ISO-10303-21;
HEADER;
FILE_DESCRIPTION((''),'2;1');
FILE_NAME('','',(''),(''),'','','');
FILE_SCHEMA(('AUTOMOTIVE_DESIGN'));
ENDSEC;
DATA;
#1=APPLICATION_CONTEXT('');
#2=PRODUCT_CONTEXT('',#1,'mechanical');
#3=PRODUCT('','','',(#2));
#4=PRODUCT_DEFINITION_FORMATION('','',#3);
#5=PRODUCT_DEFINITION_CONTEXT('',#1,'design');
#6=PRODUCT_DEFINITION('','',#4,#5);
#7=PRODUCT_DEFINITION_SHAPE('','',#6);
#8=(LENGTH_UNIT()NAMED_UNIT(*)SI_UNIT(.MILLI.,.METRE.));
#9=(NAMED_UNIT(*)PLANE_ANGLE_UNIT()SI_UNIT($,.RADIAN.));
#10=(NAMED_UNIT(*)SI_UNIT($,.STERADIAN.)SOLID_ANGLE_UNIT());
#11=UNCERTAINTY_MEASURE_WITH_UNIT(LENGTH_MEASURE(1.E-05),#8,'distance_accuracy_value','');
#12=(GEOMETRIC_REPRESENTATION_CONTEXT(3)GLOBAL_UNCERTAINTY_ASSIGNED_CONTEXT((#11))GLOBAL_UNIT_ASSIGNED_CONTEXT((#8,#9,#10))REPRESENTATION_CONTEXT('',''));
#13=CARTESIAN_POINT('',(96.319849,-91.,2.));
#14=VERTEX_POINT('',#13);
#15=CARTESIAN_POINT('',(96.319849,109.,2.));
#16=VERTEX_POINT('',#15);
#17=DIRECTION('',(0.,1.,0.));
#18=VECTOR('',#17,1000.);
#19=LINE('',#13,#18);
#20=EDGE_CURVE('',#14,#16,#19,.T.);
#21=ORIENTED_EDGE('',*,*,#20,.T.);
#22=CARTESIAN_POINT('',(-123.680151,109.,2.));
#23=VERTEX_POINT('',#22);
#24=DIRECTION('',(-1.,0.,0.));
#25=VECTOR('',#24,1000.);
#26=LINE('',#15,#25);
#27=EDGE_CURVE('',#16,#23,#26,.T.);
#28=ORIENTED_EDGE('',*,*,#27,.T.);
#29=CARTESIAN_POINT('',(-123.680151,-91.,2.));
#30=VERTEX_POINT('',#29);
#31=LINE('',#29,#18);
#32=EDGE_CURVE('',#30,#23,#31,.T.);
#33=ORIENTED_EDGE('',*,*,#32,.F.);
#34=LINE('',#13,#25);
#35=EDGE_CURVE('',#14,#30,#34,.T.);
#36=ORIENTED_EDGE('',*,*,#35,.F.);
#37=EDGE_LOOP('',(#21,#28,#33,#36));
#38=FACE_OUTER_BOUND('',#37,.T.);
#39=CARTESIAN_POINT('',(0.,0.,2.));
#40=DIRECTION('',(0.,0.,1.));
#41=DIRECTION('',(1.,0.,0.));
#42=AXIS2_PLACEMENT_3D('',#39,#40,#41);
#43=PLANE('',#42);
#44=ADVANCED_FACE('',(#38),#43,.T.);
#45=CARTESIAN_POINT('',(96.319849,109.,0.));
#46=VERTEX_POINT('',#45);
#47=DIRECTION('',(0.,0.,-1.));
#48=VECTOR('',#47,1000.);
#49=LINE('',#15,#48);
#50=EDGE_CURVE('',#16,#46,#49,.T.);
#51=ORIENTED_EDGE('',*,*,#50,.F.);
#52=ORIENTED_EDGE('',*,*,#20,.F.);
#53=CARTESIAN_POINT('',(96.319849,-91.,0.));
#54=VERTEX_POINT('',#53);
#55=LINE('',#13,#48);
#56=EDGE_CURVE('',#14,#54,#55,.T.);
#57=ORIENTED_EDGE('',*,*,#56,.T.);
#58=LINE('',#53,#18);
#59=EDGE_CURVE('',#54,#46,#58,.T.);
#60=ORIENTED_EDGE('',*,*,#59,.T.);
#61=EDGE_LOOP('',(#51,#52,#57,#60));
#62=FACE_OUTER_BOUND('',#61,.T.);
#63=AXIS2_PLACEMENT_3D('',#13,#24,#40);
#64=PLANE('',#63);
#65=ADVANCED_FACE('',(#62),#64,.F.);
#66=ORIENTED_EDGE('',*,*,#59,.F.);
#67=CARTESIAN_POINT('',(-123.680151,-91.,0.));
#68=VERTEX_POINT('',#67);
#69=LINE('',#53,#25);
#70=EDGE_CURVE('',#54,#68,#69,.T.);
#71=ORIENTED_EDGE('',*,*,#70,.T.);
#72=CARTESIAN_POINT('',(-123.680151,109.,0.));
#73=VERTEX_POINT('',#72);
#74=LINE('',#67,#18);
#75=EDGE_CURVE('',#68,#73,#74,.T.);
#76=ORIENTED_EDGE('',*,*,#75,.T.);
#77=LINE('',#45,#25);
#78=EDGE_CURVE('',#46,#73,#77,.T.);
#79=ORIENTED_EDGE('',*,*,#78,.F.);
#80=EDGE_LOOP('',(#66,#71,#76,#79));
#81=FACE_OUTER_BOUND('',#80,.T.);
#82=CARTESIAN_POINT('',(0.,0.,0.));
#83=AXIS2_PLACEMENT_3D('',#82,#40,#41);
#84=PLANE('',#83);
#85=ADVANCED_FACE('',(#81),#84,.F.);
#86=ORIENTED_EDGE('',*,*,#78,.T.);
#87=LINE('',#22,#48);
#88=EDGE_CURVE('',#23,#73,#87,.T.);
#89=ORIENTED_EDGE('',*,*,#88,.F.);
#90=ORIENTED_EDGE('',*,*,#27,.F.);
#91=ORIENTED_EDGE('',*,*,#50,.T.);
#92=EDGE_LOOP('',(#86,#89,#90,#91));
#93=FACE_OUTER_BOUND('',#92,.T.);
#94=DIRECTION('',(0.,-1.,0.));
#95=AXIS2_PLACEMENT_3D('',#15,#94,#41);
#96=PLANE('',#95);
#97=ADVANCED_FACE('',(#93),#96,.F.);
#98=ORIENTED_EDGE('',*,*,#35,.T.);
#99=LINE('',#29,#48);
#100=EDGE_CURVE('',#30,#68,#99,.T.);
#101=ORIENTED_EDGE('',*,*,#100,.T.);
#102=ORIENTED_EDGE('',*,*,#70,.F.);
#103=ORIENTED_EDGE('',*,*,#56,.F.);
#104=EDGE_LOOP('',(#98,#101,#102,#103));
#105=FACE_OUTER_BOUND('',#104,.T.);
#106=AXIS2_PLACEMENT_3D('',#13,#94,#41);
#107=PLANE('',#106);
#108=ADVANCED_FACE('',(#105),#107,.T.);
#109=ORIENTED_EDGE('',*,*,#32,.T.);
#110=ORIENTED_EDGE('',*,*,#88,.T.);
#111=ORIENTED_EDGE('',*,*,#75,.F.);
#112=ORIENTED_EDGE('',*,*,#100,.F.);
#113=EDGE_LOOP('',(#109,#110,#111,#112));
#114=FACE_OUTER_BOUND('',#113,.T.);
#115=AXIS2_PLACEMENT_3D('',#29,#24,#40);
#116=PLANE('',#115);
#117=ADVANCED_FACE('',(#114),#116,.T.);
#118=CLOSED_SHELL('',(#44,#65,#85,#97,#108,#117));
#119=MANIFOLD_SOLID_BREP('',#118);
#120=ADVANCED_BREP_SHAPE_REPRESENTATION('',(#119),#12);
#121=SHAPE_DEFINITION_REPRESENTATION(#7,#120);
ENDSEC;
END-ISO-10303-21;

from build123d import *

# Parameters (mm, degrees)
SKETCH1_W           = 220
SKETCH1_H           = 200
BOSS_EXTRUDE1_DEPTH = 2


with BuildPart() as part:
    # Sketch1 → Boss-Extrude1 (new body)
    with BuildSketch(Plane.XY):
        with Locations((-13.680151025, 9)):
            Rectangle(SKETCH1_W, SKETCH1_H)
    extrude(amount=BOSS_EXTRUDE1_DEPTH)


solid = part.part
